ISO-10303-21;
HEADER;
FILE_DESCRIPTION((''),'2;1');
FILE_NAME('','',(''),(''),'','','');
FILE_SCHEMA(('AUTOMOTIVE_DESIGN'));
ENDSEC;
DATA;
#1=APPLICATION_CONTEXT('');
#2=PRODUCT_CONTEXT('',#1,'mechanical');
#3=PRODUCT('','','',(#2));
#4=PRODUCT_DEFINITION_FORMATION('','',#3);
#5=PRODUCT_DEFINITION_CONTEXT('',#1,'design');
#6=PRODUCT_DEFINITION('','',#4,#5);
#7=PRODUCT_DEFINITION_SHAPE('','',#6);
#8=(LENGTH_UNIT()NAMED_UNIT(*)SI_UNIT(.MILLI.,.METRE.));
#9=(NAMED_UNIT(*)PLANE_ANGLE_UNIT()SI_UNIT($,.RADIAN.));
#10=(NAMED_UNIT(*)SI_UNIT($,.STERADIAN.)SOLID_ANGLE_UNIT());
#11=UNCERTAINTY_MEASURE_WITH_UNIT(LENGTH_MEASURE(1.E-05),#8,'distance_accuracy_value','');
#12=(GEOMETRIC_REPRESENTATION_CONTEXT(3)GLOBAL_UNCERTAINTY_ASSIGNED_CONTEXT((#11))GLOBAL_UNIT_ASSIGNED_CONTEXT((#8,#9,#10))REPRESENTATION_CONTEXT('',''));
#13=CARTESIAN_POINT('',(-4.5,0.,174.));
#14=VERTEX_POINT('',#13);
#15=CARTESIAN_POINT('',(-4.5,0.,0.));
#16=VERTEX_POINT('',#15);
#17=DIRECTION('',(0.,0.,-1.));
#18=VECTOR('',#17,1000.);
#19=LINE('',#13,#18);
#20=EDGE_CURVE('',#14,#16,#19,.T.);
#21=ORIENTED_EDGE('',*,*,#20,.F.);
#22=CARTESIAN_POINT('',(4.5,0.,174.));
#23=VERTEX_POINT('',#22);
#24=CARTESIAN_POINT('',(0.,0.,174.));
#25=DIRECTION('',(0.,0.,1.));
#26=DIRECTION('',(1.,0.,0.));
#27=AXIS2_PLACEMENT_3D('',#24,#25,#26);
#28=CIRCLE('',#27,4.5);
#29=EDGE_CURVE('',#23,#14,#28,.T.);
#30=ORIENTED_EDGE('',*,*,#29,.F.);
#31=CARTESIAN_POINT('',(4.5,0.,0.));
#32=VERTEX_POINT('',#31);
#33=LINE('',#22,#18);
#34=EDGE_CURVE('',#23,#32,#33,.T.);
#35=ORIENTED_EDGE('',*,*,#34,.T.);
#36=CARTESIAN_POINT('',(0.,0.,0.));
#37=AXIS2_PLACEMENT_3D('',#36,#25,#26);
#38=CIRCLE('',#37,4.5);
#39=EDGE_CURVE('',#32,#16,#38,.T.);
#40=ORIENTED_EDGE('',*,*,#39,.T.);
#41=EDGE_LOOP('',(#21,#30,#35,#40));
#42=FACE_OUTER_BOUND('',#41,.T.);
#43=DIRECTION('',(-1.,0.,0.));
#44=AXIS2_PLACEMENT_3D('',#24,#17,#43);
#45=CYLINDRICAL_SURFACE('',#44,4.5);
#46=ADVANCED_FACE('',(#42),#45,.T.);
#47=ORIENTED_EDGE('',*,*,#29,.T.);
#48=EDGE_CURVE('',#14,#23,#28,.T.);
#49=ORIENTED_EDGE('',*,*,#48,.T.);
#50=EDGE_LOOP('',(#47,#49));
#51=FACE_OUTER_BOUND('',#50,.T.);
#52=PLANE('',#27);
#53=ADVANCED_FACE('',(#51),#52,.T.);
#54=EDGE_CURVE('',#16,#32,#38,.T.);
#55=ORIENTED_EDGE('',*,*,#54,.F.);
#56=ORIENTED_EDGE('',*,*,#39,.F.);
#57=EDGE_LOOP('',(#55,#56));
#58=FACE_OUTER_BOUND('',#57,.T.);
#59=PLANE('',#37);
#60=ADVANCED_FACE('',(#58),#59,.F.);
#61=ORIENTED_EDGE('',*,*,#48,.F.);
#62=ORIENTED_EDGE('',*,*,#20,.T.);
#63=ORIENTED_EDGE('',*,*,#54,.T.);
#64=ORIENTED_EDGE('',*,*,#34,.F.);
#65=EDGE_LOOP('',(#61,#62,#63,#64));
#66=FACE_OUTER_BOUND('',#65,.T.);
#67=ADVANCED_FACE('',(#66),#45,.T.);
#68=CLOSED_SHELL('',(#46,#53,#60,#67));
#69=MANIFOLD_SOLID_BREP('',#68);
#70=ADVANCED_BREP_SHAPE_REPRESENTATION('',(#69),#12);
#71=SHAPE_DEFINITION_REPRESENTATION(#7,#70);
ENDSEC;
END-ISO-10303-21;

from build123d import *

# Parameters (mm, degrees)
SKETCH1_R           = 4.5
BOSS_EXTRUDE1_DEPTH = 174


with BuildPart() as part:
    # Sketch1 → Boss-Extrude1 (new body)
    with BuildSketch(Plane.XY):
        Circle(SKETCH1_R)
    extrude(amount=BOSS_EXTRUDE1_DEPTH)


solid = part.part
